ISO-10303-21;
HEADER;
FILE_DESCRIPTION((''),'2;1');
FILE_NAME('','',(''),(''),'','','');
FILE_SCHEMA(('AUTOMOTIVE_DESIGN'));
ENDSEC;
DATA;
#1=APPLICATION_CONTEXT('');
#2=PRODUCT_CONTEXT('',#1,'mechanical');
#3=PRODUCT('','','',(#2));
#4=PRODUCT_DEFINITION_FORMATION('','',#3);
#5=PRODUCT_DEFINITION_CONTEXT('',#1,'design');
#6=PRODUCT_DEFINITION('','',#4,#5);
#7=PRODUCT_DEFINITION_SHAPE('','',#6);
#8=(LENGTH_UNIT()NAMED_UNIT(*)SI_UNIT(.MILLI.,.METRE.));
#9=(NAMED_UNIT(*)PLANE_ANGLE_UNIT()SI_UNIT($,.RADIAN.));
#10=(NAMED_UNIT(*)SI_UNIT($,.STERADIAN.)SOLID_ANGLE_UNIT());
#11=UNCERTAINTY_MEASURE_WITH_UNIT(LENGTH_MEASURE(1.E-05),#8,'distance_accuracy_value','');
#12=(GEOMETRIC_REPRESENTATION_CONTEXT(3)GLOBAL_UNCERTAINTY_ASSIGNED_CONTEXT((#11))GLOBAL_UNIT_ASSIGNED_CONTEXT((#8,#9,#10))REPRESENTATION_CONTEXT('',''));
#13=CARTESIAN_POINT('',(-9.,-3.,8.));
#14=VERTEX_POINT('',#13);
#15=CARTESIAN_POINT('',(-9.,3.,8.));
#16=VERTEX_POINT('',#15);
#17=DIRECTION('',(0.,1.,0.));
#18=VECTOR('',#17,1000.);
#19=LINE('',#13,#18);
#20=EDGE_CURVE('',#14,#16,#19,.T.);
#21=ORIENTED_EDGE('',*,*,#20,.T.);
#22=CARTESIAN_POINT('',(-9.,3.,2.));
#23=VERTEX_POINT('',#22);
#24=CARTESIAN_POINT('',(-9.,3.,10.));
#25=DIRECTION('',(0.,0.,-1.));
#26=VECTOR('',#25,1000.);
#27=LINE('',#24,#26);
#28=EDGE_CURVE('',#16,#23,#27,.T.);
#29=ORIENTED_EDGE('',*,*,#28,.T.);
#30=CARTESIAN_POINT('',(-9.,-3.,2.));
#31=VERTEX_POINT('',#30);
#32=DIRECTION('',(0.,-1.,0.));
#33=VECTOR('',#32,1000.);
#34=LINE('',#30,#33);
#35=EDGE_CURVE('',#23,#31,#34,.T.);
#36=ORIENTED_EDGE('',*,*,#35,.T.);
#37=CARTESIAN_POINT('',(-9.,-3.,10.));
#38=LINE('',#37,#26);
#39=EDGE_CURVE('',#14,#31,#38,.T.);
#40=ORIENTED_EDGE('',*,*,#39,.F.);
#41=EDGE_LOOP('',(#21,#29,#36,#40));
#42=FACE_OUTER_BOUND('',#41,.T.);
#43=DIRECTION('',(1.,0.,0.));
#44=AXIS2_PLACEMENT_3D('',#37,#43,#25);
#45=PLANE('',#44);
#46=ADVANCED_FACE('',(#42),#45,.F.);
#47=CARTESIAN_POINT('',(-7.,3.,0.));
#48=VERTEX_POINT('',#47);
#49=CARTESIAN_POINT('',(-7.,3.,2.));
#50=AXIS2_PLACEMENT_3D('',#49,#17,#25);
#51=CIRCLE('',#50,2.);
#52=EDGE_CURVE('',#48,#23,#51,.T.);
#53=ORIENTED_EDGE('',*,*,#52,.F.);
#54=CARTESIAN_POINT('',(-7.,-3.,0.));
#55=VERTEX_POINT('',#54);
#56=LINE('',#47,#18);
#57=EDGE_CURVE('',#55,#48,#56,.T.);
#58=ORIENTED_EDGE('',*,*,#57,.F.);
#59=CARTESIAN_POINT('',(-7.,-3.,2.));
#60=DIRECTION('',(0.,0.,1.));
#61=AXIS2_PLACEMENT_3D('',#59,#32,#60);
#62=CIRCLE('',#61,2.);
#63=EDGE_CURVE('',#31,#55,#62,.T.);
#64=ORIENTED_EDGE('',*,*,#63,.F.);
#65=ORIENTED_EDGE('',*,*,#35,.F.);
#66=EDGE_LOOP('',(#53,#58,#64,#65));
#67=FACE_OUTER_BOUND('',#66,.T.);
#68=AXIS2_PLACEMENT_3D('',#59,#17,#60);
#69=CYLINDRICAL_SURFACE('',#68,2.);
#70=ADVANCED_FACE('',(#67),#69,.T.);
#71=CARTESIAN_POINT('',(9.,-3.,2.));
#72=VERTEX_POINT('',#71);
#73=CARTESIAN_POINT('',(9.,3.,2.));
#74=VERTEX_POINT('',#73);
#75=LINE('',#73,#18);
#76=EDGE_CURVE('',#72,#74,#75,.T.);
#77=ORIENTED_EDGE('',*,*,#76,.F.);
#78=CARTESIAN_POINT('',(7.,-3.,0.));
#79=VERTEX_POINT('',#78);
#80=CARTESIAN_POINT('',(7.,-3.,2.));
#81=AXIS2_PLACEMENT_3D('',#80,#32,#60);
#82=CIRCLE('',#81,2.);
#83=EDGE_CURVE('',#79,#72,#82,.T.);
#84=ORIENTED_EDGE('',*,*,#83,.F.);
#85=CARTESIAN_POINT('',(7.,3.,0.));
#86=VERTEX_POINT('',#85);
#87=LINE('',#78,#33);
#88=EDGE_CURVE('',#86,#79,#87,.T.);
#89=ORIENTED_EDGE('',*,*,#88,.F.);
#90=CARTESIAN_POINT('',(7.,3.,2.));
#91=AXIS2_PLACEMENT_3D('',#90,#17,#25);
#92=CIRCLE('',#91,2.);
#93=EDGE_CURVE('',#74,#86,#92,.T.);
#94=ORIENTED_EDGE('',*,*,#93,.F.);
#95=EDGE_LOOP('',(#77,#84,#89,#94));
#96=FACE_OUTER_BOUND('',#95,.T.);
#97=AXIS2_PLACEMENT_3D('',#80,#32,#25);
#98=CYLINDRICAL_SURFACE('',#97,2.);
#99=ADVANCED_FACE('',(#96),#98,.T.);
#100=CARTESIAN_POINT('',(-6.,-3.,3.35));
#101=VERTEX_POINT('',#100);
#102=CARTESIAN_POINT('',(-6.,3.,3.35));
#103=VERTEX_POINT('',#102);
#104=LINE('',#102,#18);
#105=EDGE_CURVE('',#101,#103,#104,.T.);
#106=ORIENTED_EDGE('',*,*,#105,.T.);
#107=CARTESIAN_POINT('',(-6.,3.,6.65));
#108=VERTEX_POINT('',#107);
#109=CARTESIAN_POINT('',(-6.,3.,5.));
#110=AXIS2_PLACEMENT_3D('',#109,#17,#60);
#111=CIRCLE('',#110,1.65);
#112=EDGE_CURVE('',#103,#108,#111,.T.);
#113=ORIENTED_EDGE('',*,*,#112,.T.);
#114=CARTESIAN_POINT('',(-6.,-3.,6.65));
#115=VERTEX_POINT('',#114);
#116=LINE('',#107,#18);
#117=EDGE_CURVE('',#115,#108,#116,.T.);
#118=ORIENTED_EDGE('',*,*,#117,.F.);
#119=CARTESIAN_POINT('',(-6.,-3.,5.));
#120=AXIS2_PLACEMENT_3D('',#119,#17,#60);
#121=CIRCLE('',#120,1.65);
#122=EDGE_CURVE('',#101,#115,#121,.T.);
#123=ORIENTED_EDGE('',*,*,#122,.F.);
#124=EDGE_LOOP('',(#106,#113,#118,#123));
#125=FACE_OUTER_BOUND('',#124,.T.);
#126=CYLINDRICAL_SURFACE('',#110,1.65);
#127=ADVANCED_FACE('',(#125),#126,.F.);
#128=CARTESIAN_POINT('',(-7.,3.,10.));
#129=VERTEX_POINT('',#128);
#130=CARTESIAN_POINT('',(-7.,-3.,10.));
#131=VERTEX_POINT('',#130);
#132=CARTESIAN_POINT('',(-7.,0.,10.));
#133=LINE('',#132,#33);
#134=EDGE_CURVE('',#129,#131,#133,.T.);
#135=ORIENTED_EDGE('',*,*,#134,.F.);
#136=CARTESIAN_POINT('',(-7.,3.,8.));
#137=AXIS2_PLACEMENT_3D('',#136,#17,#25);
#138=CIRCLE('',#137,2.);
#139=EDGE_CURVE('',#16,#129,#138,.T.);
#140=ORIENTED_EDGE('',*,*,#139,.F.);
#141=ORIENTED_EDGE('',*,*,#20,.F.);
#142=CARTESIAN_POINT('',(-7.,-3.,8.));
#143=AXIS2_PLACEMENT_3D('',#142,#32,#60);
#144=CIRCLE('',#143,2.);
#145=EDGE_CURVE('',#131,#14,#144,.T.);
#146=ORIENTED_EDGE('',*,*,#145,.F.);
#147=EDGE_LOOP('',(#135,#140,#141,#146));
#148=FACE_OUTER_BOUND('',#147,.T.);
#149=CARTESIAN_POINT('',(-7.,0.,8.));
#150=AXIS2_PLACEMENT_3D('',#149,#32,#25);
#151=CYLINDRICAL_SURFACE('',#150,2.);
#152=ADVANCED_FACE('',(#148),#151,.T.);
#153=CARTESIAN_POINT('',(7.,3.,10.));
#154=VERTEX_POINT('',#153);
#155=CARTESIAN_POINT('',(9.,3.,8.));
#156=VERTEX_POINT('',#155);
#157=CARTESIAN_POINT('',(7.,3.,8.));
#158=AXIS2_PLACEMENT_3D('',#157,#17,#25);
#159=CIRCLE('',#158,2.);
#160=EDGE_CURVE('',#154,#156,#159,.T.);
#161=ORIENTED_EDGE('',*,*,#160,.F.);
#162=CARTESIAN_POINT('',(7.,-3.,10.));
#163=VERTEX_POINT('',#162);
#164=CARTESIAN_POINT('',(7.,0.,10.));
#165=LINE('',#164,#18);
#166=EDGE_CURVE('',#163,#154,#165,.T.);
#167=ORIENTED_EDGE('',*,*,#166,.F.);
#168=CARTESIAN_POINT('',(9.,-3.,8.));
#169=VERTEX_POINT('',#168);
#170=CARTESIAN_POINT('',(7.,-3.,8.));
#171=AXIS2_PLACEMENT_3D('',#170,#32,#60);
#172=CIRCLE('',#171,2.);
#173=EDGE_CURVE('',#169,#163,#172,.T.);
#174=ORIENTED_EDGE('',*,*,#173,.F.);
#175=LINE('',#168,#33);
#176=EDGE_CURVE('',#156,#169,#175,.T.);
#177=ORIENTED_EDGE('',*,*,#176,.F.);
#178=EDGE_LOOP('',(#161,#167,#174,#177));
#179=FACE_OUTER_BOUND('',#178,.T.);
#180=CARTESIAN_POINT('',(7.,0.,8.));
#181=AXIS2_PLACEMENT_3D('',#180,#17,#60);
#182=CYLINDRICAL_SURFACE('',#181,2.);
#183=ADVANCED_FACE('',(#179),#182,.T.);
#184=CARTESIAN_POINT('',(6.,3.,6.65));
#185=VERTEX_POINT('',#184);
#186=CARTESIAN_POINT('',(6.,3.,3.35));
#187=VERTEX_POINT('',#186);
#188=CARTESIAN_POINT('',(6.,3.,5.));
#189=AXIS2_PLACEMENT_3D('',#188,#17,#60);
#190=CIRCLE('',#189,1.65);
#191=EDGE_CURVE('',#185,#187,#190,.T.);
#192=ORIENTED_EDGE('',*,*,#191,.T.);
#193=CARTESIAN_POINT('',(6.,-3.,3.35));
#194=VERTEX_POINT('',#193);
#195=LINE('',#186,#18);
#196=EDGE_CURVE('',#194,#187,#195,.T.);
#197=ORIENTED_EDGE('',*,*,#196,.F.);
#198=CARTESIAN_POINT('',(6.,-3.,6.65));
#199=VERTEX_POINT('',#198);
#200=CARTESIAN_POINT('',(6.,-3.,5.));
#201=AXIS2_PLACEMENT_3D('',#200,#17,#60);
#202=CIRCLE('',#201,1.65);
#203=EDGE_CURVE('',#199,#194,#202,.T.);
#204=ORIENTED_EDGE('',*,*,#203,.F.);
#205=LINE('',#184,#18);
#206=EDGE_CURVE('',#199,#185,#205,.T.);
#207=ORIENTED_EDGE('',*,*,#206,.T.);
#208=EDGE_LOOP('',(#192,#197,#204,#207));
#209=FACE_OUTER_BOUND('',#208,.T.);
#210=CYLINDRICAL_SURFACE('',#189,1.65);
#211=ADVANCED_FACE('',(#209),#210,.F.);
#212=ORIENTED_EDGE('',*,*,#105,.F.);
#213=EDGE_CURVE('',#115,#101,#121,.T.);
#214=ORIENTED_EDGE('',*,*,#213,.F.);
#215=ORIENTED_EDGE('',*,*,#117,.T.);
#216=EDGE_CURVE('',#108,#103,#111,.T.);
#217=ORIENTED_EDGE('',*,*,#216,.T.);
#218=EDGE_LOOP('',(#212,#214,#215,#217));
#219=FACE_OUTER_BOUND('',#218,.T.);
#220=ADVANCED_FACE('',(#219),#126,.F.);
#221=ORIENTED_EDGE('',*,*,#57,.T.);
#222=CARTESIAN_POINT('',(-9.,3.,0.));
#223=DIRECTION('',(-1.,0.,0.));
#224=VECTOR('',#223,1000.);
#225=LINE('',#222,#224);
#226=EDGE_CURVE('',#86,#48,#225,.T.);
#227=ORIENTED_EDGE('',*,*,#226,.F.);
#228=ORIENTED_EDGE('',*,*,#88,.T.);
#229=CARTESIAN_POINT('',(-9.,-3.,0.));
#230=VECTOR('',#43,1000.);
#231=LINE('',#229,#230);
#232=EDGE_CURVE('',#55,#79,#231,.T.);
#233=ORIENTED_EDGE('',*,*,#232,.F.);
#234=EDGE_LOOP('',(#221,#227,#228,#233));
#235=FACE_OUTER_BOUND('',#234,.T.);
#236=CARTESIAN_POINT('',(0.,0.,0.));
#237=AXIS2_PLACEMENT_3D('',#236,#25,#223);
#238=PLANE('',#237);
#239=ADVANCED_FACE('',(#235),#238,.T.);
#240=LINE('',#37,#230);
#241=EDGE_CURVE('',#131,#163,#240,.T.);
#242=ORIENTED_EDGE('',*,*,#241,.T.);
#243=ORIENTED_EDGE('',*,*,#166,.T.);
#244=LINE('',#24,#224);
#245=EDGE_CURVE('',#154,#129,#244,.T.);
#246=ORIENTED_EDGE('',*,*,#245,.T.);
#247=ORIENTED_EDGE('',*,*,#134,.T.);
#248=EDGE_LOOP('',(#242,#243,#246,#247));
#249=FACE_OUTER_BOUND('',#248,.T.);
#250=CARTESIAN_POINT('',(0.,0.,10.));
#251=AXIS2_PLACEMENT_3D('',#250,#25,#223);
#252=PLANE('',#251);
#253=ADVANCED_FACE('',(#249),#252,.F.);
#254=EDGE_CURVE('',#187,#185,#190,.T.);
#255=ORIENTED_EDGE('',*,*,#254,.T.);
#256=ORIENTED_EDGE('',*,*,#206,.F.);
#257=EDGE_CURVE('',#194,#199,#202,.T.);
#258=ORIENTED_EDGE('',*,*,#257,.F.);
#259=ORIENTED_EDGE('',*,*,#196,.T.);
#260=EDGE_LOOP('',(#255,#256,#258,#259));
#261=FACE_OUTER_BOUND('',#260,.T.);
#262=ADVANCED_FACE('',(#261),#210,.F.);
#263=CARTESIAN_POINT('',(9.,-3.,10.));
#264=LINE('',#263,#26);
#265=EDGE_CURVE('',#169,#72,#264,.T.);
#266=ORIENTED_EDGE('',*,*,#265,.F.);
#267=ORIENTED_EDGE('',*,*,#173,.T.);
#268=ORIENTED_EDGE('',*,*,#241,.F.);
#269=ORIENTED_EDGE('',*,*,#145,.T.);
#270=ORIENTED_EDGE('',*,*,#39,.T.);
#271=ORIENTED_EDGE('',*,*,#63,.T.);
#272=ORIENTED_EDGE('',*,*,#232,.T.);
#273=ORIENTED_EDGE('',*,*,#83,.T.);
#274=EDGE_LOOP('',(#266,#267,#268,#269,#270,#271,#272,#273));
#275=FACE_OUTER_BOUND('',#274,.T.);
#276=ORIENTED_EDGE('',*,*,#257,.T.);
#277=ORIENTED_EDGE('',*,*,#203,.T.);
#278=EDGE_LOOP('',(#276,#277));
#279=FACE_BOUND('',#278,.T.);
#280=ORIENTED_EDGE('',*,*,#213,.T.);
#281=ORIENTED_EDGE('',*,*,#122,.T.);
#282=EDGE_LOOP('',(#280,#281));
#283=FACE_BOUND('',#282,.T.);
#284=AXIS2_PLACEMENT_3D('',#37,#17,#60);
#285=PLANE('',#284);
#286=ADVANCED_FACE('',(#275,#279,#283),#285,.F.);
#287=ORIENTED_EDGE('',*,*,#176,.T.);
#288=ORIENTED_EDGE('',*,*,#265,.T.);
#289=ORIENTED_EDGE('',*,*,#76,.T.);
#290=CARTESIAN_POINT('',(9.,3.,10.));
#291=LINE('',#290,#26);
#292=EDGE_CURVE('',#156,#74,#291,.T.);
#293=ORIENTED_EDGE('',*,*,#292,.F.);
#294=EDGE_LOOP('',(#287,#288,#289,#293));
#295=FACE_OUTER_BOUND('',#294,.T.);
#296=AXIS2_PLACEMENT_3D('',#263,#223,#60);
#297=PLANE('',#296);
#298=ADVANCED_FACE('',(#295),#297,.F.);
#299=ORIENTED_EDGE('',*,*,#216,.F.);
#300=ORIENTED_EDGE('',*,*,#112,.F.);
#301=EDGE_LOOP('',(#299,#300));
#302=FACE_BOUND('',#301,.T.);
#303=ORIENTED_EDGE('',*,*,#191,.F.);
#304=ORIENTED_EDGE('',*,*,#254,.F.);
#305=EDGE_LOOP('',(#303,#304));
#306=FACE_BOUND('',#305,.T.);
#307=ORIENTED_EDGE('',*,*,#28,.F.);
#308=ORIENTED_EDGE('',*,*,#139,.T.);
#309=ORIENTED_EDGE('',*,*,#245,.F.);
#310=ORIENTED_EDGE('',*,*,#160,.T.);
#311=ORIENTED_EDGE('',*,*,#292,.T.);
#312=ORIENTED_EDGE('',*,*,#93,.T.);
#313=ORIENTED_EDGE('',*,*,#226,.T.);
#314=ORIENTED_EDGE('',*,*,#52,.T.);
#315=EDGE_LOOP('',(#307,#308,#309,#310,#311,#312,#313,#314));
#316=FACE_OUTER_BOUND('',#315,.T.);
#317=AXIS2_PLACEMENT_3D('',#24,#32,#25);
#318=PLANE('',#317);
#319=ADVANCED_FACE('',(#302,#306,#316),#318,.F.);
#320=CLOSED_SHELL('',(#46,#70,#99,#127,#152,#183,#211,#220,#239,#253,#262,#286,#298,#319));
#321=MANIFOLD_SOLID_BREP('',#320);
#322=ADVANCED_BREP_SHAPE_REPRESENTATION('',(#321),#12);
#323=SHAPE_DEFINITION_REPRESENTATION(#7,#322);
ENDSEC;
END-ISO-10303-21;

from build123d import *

# Parameters (mm, degrees)
SKETCH_1_W         = 18
SKETCH_1_H         = 6
EXTRUDE_1_DEPTH    = 10
HOLE_WIZARD_M4_3_D = 3.3
FILLET_1_R         = 2


with BuildPart() as part:
    # 草图1 → 凸台-拉伸1 (new body)
    with BuildSketch(Plane.XY):
        Rectangle(SKETCH_1_W, SKETCH_1_H)
    extrude(amount=EXTRUDE_1_DEPTH)

    # M4 螺纹孔3 (through all)
    with Locations(Plane(origin=(0, 3, 0), x_dir=(1, 0, 0), z_dir=(0, 1, 0))):
        with Locations((6, -5), (-6, -5)):
            Hole(HOLE_WIZARD_M4_3_D / 2)

    # 圆角1
    fillet_1_edges = [part.edges().sort_by_distance(p)[0] for p in [
        (-9, 0, 10),
        (9, 0, 10),
        (-9, 0, 0),
        (9, 0, 0),
    ]]
    fillet(fillet_1_edges, radius=FILLET_1_R)


solid = part.part
